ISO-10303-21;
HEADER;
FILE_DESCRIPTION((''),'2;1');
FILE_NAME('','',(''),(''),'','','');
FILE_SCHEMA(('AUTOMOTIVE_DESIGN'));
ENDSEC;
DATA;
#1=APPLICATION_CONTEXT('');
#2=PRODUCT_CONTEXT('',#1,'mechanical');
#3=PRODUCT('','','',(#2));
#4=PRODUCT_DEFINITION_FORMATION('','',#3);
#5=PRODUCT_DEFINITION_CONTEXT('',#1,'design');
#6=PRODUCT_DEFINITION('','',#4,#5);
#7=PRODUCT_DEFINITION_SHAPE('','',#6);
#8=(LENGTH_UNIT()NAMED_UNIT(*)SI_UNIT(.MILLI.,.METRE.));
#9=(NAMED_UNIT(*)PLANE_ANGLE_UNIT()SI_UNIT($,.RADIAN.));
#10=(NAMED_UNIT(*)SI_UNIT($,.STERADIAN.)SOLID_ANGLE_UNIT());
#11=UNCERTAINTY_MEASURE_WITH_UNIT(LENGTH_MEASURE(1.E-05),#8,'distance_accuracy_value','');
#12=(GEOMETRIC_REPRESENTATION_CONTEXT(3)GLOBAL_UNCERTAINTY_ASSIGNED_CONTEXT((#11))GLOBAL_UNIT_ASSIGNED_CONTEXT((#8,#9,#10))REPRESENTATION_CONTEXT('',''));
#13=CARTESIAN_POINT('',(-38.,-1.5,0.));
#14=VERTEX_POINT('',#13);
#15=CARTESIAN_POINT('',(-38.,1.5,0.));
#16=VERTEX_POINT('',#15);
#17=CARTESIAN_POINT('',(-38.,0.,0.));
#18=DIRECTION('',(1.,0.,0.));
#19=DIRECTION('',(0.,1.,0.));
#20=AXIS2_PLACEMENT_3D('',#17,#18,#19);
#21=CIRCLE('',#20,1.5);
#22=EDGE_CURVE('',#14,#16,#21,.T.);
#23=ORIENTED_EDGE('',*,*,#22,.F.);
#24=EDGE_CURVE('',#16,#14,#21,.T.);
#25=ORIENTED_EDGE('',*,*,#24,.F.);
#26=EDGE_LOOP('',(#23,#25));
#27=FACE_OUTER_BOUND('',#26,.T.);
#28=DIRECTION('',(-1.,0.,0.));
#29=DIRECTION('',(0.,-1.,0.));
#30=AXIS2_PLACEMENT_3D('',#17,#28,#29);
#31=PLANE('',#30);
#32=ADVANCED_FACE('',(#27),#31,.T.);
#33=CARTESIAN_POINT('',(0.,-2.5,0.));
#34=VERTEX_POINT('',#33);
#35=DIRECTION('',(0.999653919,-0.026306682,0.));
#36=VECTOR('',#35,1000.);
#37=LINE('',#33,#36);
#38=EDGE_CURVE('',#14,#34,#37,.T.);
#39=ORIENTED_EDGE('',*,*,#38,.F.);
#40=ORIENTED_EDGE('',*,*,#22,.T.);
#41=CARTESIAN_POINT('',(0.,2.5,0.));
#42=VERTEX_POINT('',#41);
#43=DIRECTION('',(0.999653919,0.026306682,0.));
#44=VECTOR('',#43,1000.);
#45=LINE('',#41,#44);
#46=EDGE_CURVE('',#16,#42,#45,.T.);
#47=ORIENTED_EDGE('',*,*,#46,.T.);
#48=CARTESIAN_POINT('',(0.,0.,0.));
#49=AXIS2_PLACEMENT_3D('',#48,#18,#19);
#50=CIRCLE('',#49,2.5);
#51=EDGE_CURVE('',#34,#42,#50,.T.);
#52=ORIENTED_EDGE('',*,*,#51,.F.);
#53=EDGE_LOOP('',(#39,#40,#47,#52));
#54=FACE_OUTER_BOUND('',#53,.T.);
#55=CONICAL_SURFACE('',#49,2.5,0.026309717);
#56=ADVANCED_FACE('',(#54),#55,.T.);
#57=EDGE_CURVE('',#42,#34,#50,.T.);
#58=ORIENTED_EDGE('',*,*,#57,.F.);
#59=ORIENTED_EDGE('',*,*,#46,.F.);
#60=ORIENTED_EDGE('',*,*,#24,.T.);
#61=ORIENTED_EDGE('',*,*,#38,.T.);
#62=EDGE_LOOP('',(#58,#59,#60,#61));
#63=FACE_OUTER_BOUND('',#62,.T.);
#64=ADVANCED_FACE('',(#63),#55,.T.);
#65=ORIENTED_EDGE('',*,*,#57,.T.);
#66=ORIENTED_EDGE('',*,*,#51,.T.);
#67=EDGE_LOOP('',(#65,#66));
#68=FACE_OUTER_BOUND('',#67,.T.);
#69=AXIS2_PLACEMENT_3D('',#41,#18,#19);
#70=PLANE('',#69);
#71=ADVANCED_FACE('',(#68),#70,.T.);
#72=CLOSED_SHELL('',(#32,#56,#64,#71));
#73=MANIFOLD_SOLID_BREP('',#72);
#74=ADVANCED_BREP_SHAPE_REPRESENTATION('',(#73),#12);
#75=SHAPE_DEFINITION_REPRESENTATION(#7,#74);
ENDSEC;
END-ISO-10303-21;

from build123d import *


with BuildPart() as part:
    # Taper Pin Profile → Taper Pin Ø5-Ø3 x 38 (revolve)
    with BuildSketch(Plane.XY):
        Polygon((0, 0), (-38, 0), (-38, 1.5), (0, 2.5), align=None)
    revolve(axis=Axis((0, 0, 0), (-1, 0, 0)))


solid = part.part
